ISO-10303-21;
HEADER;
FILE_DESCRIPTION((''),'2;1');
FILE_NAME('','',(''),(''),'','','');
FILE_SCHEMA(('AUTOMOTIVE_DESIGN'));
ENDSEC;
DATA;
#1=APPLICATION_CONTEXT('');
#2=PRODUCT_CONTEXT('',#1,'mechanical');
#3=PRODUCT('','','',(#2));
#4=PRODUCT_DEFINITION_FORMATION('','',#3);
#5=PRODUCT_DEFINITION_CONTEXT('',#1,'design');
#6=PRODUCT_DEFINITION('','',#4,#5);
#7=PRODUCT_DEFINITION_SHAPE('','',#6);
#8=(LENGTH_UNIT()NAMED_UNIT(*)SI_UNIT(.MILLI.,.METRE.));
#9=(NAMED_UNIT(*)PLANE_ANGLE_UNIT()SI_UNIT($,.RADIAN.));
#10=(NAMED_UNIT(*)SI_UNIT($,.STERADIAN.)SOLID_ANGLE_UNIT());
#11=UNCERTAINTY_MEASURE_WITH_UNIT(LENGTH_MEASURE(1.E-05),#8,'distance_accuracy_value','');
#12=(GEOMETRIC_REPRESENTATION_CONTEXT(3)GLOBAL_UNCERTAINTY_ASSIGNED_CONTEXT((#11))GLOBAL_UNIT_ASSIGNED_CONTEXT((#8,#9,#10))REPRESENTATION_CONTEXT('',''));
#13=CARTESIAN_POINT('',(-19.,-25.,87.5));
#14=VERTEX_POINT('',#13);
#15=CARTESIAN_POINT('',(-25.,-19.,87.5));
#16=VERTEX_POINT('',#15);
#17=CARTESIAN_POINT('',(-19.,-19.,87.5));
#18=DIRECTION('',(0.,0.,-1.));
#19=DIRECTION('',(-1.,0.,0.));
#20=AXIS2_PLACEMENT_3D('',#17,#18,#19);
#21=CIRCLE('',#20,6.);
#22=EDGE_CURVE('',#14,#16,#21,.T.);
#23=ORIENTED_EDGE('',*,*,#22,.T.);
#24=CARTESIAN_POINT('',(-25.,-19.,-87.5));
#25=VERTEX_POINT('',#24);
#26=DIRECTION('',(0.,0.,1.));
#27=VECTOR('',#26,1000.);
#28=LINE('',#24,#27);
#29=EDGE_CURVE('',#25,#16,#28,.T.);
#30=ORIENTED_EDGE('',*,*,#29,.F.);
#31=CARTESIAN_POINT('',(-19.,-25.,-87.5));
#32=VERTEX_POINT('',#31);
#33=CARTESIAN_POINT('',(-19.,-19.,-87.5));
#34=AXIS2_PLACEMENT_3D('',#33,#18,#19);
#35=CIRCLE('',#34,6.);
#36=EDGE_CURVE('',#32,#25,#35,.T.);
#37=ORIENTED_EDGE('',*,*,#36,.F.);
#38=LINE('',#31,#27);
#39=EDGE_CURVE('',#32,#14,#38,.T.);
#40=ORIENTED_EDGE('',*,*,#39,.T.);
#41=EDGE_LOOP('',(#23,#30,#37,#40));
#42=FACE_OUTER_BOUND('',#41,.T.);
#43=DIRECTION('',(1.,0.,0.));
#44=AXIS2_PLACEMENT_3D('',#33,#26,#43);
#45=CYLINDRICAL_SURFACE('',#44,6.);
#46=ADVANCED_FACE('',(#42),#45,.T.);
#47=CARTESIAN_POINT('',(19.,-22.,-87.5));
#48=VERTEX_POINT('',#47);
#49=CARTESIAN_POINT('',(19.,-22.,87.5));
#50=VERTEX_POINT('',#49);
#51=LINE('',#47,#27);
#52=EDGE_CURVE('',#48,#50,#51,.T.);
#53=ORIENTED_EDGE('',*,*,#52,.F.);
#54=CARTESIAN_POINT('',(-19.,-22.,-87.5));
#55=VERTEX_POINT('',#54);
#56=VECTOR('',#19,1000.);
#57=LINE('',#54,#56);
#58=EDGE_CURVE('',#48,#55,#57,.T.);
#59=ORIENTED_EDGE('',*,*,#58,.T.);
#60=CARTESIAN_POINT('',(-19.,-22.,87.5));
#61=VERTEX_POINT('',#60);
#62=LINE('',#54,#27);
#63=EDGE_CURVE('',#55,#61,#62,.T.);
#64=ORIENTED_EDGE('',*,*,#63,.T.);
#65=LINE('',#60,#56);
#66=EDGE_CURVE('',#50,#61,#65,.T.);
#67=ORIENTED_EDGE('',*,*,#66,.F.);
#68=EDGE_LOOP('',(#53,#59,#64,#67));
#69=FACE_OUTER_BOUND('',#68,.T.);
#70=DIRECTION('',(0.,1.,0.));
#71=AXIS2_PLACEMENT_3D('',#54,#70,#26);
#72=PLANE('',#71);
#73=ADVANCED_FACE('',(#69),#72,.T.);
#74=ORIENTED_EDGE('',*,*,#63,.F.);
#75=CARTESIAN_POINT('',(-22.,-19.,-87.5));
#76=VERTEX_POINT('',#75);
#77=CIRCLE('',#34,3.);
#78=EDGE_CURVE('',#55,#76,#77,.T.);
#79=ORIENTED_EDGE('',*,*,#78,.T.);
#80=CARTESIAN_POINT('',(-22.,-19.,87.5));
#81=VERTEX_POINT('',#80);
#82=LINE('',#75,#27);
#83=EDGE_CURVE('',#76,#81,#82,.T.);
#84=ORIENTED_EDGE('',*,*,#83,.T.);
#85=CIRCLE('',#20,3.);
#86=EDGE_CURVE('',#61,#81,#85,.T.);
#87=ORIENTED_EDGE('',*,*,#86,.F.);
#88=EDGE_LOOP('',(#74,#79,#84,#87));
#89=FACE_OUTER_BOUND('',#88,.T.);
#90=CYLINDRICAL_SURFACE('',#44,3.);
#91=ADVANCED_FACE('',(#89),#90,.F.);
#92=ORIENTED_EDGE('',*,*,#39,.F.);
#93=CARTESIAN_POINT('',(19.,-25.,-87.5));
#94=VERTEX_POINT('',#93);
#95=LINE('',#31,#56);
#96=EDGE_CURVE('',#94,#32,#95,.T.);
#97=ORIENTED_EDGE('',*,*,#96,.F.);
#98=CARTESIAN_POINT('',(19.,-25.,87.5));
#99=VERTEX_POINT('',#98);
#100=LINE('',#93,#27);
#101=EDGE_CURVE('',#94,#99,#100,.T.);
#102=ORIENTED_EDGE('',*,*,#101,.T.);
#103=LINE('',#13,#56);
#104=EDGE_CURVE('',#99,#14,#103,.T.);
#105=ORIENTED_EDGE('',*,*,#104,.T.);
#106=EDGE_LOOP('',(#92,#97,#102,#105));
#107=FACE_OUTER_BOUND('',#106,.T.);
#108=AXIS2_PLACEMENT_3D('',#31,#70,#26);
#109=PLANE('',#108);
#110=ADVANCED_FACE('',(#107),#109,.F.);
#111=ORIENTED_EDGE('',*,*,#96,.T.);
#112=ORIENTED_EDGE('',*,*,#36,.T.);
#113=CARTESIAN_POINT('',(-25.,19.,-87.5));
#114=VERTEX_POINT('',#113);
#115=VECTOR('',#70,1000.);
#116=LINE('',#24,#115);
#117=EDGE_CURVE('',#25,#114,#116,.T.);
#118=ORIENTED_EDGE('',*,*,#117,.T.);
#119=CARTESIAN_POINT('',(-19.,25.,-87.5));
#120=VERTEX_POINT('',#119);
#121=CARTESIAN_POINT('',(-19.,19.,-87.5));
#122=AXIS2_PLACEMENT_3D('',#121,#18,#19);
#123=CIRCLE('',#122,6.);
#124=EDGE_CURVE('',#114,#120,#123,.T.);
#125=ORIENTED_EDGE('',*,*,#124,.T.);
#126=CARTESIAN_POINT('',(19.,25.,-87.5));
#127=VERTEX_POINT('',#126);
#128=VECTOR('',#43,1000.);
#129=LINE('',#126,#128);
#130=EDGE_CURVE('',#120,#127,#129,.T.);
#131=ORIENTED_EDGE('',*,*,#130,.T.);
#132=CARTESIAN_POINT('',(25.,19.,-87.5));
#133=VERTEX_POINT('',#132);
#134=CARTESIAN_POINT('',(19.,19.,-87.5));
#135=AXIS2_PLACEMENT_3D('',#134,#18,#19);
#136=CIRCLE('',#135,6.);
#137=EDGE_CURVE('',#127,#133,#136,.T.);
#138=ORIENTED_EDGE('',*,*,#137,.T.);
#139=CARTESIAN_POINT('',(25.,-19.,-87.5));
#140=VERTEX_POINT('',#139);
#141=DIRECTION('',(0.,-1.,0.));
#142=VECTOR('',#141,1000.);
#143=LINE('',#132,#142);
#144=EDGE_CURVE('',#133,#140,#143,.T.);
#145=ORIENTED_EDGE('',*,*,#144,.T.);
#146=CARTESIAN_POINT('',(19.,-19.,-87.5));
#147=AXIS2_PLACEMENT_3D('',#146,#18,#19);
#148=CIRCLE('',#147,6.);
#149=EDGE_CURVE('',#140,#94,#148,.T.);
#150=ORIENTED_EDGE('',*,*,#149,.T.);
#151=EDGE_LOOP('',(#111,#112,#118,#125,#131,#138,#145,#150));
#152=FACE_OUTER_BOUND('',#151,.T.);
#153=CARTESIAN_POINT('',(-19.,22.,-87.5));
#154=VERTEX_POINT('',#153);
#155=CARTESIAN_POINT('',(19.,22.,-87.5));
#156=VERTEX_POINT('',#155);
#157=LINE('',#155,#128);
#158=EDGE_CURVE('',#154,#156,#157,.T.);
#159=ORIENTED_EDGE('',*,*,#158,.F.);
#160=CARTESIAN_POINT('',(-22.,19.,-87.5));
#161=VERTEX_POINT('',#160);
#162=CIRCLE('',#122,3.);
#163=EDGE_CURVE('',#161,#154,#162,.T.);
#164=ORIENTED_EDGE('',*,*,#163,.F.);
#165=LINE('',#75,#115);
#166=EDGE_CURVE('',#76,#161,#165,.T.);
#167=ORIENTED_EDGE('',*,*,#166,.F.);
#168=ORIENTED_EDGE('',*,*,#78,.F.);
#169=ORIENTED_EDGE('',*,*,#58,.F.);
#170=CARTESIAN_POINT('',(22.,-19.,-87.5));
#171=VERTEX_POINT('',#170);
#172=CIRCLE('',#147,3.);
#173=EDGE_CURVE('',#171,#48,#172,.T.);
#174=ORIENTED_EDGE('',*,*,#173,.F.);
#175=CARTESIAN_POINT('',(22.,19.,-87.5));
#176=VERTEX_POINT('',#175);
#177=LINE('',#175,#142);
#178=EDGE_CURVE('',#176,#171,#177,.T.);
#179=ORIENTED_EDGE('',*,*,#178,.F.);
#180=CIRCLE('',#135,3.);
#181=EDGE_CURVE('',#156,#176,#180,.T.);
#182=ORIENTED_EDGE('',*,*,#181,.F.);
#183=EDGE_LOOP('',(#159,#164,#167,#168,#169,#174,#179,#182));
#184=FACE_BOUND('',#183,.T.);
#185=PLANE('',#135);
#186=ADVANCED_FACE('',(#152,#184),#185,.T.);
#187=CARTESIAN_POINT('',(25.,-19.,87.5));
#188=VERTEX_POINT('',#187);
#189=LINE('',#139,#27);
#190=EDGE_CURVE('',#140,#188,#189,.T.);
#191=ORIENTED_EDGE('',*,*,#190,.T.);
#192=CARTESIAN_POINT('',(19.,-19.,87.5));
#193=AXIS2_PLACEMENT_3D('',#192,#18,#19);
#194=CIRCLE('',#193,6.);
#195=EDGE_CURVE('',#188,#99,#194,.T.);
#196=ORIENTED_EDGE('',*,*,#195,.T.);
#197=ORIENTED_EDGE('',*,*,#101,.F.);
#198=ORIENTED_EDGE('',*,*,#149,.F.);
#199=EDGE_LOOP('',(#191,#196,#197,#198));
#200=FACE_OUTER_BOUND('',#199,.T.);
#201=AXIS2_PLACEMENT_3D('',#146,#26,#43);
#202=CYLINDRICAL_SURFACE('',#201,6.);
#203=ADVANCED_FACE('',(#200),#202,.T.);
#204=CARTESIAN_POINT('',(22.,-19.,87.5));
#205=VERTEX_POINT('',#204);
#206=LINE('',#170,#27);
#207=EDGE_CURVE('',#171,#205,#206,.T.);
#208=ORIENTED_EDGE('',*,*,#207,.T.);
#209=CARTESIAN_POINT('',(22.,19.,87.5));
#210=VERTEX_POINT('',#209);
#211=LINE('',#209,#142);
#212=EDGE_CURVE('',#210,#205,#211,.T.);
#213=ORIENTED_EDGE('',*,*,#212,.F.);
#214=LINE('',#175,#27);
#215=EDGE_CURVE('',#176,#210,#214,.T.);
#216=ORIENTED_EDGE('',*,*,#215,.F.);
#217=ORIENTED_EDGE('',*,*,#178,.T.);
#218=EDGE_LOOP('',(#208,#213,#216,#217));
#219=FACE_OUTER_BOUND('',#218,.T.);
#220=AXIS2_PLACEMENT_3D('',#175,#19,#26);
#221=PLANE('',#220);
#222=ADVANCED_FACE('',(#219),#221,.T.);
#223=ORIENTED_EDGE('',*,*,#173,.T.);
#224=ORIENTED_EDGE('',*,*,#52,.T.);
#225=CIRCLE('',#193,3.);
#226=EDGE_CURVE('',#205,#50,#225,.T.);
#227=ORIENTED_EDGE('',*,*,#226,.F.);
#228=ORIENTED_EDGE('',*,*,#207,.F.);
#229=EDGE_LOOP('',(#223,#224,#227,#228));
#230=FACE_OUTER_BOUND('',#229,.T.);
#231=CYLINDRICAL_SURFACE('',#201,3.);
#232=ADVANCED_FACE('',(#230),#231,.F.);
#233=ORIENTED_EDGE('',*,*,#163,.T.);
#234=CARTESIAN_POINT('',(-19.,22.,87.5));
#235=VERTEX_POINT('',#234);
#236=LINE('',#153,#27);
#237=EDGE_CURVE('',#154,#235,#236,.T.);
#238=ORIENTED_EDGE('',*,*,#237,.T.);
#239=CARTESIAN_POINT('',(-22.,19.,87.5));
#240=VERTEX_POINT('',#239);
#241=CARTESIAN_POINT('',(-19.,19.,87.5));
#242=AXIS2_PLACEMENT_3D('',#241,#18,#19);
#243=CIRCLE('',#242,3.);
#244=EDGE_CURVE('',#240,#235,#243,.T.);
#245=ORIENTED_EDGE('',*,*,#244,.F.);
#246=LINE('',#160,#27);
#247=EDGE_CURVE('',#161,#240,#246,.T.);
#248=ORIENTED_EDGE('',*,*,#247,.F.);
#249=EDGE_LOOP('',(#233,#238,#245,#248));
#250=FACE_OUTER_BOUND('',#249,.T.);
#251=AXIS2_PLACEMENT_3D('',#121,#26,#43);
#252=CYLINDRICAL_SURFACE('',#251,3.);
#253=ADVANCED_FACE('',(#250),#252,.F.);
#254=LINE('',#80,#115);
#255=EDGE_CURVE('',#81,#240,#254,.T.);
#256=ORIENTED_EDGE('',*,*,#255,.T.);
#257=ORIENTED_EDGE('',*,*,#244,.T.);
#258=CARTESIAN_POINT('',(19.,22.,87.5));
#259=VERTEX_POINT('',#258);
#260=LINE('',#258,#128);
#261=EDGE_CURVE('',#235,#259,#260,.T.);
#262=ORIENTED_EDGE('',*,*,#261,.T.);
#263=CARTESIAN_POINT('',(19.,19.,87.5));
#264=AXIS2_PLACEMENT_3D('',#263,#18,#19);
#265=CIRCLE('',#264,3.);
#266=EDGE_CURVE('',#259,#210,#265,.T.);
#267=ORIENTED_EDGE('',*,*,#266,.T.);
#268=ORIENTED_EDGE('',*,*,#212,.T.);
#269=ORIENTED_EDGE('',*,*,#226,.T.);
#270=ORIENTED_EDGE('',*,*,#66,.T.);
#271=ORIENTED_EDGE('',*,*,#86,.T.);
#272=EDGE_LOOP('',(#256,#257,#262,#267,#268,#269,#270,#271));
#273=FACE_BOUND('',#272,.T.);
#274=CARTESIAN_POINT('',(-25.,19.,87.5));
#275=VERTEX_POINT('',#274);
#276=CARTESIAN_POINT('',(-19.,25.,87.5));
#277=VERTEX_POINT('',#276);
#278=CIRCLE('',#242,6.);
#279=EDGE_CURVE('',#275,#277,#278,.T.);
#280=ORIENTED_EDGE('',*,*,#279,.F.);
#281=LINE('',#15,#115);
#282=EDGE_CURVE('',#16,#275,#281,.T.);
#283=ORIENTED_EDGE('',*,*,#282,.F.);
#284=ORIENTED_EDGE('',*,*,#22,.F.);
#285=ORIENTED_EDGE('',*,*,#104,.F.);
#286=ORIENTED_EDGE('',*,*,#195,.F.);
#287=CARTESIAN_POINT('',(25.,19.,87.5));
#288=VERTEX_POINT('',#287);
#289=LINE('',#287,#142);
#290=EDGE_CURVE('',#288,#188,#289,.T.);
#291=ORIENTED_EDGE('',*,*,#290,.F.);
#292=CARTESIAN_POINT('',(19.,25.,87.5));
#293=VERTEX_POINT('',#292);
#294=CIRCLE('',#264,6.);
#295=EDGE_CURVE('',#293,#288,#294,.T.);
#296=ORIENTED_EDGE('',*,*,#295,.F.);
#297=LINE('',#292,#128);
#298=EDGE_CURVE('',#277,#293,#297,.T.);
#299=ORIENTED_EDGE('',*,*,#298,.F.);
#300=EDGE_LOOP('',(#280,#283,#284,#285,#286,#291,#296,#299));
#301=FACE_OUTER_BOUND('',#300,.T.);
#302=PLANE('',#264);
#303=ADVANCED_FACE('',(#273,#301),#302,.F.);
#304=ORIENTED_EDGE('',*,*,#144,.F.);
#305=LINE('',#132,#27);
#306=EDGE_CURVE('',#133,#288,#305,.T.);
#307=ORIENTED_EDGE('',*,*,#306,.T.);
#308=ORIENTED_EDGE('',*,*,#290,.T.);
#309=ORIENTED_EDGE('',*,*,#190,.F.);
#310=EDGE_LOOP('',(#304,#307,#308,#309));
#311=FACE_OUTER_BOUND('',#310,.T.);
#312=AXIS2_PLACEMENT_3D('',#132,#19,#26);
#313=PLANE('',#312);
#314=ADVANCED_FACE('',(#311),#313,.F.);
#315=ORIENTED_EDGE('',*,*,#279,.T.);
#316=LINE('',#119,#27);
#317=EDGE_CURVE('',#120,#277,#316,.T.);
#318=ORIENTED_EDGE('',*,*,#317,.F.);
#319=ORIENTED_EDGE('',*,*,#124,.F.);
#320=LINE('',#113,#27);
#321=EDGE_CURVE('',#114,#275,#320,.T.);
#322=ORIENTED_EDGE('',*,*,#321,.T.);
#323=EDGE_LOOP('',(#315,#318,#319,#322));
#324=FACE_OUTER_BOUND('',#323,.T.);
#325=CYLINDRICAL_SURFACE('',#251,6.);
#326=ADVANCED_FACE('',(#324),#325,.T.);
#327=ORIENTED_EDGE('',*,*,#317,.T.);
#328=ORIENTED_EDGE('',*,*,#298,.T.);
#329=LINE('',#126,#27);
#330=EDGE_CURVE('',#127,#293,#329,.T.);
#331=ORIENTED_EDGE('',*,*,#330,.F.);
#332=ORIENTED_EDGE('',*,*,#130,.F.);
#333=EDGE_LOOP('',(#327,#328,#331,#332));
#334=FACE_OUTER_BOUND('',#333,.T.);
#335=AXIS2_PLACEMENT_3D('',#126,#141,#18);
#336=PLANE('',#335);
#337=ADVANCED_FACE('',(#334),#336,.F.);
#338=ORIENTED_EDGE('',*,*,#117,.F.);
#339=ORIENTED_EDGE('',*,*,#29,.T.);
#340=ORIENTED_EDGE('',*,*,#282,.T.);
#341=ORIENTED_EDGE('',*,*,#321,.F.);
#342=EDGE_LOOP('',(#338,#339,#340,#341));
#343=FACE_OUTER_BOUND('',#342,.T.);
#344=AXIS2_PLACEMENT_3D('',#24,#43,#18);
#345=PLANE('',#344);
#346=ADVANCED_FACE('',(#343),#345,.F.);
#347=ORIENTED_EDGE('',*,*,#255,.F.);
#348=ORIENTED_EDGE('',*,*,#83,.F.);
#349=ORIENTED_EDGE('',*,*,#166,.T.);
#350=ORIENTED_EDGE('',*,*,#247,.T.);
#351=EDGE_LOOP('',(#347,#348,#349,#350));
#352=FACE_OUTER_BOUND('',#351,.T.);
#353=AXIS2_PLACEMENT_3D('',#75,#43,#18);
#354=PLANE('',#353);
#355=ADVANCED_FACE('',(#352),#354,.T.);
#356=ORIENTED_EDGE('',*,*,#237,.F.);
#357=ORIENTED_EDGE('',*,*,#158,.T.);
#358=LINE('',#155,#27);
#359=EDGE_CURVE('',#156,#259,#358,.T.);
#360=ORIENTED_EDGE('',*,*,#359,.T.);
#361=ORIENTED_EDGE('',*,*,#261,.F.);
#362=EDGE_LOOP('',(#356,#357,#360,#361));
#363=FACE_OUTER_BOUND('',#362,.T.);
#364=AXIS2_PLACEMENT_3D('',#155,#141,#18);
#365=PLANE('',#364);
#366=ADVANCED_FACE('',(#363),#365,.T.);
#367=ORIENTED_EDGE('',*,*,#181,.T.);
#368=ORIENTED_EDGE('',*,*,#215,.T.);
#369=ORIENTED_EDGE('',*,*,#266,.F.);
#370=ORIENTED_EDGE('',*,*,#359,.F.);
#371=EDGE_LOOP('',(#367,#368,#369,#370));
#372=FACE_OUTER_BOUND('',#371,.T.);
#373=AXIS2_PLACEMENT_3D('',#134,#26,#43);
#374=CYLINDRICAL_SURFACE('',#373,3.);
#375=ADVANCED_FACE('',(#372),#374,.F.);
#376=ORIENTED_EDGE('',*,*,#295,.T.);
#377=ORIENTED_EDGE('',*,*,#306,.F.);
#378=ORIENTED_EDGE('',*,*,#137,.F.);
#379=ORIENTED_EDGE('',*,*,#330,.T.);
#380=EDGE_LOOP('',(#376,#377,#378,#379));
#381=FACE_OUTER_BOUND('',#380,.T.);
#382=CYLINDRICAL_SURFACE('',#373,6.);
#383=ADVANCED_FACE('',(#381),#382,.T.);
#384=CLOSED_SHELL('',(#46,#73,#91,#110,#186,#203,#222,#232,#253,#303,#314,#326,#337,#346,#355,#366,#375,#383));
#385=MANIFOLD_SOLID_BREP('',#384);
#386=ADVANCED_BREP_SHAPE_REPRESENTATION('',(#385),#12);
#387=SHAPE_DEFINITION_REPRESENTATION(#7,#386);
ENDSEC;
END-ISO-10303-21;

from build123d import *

# Parameters (mm, degrees)
GB_6728_1986_050_X_50_X_3_1_DEPTH = 175


with BuildPart() as part:
    # Sketch1 → Gb／6728-1986方形空心型钢 050 X 50 X 3(1) (new body)
    with BuildSketch(Plane.YX.offset(-87.5)):
        with BuildLine():
            Line((-19, -25), (19, -25))
            ThreePointArc((19, -25), (23.242640687, -23.242640687), (25, -19))
            Line((25, -19), (25, 19))
            ThreePointArc((25, 19), (23.242640687, 23.242640687), (19, 25))
            Line((19, 25), (-19, 25))
            ThreePointArc((-19, 25), (-23.242640687, 23.242640687), (-25, 19))
            Line((-25, 19), (-25, -19))
            ThreePointArc((-25, -19), (-23.242640687, -23.242640687), (-19, -25))
        make_face()
        with BuildLine():
            Line((-19, -22), (19, -22))
            ThreePointArc((19, -22), (21.121320344, -21.121320344), (22, -19))
            Line((22, -19), (22, 19))
            ThreePointArc((22, 19), (21.121320344, 21.121320344), (19, 22))
            Line((19, 22), (-19, 22))
            ThreePointArc((-19, 22), (-21.121320344, 21.121320344), (-22, 19))
            Line((-22, 19), (-22, -19))
            ThreePointArc((-22, -19), (-21.121320344, -21.121320344), (-19, -22))
        make_face(mode=Mode.SUBTRACT)
    extrude(amount=GB_6728_1986_050_X_50_X_3_1_DEPTH)


solid = part.part
